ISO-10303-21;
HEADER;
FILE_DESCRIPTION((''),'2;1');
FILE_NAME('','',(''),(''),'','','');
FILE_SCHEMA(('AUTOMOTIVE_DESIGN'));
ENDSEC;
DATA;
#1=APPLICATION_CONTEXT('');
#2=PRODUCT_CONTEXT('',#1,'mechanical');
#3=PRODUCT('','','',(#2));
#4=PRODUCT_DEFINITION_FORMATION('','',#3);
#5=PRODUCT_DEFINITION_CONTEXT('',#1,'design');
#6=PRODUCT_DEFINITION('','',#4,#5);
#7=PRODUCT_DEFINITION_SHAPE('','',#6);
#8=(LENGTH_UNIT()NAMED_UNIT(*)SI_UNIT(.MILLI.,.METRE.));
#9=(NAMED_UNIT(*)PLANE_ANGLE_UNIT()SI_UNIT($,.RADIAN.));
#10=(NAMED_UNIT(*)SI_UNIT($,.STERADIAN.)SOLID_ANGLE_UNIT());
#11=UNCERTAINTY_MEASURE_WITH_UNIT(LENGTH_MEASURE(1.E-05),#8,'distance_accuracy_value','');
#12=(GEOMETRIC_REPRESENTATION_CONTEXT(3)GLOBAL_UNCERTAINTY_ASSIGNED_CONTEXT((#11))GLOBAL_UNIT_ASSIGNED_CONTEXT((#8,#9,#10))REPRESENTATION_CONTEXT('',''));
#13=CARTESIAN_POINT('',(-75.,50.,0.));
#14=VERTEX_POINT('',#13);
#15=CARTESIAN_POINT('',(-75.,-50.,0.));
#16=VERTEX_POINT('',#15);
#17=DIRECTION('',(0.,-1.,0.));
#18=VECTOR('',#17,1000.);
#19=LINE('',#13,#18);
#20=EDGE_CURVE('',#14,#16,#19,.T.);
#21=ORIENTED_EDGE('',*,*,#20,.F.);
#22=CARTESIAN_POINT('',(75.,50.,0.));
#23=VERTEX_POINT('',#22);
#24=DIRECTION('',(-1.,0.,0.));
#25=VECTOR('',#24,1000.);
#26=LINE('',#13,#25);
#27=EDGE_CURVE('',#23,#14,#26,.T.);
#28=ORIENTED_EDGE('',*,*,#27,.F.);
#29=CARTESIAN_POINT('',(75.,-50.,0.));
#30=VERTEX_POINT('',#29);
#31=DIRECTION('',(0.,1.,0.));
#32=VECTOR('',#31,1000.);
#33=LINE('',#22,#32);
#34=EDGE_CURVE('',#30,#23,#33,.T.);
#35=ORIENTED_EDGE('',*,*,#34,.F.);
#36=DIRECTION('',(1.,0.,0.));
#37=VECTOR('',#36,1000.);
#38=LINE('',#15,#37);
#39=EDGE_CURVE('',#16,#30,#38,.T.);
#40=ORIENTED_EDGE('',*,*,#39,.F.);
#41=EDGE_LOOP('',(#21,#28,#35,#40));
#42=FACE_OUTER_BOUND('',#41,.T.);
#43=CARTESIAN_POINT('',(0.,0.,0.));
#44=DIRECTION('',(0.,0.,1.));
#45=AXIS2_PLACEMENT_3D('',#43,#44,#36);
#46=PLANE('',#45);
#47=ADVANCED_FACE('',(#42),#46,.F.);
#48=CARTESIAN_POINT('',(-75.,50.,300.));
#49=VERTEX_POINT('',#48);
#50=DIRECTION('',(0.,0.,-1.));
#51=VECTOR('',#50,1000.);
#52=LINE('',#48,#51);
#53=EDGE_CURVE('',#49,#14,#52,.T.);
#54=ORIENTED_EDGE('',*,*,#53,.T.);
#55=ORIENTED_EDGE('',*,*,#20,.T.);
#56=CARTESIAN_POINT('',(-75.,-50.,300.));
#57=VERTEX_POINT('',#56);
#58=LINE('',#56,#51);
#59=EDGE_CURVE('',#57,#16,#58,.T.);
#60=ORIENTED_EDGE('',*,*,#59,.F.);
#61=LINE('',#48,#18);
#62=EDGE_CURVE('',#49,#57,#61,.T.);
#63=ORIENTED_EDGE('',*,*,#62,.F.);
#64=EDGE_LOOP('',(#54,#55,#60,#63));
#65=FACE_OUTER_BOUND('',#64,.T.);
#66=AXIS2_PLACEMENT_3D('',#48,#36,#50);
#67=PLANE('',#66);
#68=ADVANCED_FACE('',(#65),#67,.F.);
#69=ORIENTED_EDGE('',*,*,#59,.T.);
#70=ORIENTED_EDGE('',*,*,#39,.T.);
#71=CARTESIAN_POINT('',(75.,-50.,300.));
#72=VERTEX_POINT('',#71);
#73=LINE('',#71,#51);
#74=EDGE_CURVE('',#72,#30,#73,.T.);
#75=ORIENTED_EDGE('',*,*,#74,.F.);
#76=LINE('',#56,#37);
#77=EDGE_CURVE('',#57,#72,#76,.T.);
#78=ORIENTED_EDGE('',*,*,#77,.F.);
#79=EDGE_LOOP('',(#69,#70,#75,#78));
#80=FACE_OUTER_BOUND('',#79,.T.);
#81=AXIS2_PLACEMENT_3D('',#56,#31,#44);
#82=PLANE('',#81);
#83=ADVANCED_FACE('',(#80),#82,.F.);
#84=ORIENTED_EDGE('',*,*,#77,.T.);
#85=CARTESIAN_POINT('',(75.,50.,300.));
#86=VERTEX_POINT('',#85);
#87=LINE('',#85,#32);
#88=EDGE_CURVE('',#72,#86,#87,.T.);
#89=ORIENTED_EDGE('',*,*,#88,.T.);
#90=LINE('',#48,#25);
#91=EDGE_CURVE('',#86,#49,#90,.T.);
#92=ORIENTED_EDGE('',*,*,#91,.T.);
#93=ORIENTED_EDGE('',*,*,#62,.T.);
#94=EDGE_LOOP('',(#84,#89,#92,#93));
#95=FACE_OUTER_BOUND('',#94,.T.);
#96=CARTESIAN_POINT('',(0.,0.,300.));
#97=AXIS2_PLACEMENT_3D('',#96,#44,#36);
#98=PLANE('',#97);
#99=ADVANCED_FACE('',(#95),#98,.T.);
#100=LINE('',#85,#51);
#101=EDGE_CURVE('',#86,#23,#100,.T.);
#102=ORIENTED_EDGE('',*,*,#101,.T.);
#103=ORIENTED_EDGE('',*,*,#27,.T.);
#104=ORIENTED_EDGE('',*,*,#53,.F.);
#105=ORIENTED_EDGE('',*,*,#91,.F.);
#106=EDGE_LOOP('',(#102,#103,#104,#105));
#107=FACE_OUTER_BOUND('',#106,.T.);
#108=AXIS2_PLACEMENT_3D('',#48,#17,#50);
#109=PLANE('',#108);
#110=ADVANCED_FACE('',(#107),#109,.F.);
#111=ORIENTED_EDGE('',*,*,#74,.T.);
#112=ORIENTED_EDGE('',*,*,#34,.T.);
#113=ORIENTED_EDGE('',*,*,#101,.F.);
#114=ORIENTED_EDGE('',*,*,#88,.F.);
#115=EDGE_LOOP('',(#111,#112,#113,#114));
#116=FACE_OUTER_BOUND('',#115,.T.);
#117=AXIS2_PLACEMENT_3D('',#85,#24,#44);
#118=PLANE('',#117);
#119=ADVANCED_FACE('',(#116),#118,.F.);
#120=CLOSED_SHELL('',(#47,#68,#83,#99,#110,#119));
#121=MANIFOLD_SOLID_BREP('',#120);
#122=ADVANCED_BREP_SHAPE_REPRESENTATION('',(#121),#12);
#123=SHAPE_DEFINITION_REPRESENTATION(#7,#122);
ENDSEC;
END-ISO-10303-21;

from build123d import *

# Parameters (mm, degrees)
SKETCH1_W           = 150
SKETCH1_H           = 100
BOSS_EXTRUDE1_DEPTH = 300


with BuildPart() as part:
    # Sketch1 → Boss-Extrude1 (new body)
    with BuildSketch(Plane.XY):
        Rectangle(SKETCH1_W, SKETCH1_H)
    extrude(amount=BOSS_EXTRUDE1_DEPTH)


solid = part.part
